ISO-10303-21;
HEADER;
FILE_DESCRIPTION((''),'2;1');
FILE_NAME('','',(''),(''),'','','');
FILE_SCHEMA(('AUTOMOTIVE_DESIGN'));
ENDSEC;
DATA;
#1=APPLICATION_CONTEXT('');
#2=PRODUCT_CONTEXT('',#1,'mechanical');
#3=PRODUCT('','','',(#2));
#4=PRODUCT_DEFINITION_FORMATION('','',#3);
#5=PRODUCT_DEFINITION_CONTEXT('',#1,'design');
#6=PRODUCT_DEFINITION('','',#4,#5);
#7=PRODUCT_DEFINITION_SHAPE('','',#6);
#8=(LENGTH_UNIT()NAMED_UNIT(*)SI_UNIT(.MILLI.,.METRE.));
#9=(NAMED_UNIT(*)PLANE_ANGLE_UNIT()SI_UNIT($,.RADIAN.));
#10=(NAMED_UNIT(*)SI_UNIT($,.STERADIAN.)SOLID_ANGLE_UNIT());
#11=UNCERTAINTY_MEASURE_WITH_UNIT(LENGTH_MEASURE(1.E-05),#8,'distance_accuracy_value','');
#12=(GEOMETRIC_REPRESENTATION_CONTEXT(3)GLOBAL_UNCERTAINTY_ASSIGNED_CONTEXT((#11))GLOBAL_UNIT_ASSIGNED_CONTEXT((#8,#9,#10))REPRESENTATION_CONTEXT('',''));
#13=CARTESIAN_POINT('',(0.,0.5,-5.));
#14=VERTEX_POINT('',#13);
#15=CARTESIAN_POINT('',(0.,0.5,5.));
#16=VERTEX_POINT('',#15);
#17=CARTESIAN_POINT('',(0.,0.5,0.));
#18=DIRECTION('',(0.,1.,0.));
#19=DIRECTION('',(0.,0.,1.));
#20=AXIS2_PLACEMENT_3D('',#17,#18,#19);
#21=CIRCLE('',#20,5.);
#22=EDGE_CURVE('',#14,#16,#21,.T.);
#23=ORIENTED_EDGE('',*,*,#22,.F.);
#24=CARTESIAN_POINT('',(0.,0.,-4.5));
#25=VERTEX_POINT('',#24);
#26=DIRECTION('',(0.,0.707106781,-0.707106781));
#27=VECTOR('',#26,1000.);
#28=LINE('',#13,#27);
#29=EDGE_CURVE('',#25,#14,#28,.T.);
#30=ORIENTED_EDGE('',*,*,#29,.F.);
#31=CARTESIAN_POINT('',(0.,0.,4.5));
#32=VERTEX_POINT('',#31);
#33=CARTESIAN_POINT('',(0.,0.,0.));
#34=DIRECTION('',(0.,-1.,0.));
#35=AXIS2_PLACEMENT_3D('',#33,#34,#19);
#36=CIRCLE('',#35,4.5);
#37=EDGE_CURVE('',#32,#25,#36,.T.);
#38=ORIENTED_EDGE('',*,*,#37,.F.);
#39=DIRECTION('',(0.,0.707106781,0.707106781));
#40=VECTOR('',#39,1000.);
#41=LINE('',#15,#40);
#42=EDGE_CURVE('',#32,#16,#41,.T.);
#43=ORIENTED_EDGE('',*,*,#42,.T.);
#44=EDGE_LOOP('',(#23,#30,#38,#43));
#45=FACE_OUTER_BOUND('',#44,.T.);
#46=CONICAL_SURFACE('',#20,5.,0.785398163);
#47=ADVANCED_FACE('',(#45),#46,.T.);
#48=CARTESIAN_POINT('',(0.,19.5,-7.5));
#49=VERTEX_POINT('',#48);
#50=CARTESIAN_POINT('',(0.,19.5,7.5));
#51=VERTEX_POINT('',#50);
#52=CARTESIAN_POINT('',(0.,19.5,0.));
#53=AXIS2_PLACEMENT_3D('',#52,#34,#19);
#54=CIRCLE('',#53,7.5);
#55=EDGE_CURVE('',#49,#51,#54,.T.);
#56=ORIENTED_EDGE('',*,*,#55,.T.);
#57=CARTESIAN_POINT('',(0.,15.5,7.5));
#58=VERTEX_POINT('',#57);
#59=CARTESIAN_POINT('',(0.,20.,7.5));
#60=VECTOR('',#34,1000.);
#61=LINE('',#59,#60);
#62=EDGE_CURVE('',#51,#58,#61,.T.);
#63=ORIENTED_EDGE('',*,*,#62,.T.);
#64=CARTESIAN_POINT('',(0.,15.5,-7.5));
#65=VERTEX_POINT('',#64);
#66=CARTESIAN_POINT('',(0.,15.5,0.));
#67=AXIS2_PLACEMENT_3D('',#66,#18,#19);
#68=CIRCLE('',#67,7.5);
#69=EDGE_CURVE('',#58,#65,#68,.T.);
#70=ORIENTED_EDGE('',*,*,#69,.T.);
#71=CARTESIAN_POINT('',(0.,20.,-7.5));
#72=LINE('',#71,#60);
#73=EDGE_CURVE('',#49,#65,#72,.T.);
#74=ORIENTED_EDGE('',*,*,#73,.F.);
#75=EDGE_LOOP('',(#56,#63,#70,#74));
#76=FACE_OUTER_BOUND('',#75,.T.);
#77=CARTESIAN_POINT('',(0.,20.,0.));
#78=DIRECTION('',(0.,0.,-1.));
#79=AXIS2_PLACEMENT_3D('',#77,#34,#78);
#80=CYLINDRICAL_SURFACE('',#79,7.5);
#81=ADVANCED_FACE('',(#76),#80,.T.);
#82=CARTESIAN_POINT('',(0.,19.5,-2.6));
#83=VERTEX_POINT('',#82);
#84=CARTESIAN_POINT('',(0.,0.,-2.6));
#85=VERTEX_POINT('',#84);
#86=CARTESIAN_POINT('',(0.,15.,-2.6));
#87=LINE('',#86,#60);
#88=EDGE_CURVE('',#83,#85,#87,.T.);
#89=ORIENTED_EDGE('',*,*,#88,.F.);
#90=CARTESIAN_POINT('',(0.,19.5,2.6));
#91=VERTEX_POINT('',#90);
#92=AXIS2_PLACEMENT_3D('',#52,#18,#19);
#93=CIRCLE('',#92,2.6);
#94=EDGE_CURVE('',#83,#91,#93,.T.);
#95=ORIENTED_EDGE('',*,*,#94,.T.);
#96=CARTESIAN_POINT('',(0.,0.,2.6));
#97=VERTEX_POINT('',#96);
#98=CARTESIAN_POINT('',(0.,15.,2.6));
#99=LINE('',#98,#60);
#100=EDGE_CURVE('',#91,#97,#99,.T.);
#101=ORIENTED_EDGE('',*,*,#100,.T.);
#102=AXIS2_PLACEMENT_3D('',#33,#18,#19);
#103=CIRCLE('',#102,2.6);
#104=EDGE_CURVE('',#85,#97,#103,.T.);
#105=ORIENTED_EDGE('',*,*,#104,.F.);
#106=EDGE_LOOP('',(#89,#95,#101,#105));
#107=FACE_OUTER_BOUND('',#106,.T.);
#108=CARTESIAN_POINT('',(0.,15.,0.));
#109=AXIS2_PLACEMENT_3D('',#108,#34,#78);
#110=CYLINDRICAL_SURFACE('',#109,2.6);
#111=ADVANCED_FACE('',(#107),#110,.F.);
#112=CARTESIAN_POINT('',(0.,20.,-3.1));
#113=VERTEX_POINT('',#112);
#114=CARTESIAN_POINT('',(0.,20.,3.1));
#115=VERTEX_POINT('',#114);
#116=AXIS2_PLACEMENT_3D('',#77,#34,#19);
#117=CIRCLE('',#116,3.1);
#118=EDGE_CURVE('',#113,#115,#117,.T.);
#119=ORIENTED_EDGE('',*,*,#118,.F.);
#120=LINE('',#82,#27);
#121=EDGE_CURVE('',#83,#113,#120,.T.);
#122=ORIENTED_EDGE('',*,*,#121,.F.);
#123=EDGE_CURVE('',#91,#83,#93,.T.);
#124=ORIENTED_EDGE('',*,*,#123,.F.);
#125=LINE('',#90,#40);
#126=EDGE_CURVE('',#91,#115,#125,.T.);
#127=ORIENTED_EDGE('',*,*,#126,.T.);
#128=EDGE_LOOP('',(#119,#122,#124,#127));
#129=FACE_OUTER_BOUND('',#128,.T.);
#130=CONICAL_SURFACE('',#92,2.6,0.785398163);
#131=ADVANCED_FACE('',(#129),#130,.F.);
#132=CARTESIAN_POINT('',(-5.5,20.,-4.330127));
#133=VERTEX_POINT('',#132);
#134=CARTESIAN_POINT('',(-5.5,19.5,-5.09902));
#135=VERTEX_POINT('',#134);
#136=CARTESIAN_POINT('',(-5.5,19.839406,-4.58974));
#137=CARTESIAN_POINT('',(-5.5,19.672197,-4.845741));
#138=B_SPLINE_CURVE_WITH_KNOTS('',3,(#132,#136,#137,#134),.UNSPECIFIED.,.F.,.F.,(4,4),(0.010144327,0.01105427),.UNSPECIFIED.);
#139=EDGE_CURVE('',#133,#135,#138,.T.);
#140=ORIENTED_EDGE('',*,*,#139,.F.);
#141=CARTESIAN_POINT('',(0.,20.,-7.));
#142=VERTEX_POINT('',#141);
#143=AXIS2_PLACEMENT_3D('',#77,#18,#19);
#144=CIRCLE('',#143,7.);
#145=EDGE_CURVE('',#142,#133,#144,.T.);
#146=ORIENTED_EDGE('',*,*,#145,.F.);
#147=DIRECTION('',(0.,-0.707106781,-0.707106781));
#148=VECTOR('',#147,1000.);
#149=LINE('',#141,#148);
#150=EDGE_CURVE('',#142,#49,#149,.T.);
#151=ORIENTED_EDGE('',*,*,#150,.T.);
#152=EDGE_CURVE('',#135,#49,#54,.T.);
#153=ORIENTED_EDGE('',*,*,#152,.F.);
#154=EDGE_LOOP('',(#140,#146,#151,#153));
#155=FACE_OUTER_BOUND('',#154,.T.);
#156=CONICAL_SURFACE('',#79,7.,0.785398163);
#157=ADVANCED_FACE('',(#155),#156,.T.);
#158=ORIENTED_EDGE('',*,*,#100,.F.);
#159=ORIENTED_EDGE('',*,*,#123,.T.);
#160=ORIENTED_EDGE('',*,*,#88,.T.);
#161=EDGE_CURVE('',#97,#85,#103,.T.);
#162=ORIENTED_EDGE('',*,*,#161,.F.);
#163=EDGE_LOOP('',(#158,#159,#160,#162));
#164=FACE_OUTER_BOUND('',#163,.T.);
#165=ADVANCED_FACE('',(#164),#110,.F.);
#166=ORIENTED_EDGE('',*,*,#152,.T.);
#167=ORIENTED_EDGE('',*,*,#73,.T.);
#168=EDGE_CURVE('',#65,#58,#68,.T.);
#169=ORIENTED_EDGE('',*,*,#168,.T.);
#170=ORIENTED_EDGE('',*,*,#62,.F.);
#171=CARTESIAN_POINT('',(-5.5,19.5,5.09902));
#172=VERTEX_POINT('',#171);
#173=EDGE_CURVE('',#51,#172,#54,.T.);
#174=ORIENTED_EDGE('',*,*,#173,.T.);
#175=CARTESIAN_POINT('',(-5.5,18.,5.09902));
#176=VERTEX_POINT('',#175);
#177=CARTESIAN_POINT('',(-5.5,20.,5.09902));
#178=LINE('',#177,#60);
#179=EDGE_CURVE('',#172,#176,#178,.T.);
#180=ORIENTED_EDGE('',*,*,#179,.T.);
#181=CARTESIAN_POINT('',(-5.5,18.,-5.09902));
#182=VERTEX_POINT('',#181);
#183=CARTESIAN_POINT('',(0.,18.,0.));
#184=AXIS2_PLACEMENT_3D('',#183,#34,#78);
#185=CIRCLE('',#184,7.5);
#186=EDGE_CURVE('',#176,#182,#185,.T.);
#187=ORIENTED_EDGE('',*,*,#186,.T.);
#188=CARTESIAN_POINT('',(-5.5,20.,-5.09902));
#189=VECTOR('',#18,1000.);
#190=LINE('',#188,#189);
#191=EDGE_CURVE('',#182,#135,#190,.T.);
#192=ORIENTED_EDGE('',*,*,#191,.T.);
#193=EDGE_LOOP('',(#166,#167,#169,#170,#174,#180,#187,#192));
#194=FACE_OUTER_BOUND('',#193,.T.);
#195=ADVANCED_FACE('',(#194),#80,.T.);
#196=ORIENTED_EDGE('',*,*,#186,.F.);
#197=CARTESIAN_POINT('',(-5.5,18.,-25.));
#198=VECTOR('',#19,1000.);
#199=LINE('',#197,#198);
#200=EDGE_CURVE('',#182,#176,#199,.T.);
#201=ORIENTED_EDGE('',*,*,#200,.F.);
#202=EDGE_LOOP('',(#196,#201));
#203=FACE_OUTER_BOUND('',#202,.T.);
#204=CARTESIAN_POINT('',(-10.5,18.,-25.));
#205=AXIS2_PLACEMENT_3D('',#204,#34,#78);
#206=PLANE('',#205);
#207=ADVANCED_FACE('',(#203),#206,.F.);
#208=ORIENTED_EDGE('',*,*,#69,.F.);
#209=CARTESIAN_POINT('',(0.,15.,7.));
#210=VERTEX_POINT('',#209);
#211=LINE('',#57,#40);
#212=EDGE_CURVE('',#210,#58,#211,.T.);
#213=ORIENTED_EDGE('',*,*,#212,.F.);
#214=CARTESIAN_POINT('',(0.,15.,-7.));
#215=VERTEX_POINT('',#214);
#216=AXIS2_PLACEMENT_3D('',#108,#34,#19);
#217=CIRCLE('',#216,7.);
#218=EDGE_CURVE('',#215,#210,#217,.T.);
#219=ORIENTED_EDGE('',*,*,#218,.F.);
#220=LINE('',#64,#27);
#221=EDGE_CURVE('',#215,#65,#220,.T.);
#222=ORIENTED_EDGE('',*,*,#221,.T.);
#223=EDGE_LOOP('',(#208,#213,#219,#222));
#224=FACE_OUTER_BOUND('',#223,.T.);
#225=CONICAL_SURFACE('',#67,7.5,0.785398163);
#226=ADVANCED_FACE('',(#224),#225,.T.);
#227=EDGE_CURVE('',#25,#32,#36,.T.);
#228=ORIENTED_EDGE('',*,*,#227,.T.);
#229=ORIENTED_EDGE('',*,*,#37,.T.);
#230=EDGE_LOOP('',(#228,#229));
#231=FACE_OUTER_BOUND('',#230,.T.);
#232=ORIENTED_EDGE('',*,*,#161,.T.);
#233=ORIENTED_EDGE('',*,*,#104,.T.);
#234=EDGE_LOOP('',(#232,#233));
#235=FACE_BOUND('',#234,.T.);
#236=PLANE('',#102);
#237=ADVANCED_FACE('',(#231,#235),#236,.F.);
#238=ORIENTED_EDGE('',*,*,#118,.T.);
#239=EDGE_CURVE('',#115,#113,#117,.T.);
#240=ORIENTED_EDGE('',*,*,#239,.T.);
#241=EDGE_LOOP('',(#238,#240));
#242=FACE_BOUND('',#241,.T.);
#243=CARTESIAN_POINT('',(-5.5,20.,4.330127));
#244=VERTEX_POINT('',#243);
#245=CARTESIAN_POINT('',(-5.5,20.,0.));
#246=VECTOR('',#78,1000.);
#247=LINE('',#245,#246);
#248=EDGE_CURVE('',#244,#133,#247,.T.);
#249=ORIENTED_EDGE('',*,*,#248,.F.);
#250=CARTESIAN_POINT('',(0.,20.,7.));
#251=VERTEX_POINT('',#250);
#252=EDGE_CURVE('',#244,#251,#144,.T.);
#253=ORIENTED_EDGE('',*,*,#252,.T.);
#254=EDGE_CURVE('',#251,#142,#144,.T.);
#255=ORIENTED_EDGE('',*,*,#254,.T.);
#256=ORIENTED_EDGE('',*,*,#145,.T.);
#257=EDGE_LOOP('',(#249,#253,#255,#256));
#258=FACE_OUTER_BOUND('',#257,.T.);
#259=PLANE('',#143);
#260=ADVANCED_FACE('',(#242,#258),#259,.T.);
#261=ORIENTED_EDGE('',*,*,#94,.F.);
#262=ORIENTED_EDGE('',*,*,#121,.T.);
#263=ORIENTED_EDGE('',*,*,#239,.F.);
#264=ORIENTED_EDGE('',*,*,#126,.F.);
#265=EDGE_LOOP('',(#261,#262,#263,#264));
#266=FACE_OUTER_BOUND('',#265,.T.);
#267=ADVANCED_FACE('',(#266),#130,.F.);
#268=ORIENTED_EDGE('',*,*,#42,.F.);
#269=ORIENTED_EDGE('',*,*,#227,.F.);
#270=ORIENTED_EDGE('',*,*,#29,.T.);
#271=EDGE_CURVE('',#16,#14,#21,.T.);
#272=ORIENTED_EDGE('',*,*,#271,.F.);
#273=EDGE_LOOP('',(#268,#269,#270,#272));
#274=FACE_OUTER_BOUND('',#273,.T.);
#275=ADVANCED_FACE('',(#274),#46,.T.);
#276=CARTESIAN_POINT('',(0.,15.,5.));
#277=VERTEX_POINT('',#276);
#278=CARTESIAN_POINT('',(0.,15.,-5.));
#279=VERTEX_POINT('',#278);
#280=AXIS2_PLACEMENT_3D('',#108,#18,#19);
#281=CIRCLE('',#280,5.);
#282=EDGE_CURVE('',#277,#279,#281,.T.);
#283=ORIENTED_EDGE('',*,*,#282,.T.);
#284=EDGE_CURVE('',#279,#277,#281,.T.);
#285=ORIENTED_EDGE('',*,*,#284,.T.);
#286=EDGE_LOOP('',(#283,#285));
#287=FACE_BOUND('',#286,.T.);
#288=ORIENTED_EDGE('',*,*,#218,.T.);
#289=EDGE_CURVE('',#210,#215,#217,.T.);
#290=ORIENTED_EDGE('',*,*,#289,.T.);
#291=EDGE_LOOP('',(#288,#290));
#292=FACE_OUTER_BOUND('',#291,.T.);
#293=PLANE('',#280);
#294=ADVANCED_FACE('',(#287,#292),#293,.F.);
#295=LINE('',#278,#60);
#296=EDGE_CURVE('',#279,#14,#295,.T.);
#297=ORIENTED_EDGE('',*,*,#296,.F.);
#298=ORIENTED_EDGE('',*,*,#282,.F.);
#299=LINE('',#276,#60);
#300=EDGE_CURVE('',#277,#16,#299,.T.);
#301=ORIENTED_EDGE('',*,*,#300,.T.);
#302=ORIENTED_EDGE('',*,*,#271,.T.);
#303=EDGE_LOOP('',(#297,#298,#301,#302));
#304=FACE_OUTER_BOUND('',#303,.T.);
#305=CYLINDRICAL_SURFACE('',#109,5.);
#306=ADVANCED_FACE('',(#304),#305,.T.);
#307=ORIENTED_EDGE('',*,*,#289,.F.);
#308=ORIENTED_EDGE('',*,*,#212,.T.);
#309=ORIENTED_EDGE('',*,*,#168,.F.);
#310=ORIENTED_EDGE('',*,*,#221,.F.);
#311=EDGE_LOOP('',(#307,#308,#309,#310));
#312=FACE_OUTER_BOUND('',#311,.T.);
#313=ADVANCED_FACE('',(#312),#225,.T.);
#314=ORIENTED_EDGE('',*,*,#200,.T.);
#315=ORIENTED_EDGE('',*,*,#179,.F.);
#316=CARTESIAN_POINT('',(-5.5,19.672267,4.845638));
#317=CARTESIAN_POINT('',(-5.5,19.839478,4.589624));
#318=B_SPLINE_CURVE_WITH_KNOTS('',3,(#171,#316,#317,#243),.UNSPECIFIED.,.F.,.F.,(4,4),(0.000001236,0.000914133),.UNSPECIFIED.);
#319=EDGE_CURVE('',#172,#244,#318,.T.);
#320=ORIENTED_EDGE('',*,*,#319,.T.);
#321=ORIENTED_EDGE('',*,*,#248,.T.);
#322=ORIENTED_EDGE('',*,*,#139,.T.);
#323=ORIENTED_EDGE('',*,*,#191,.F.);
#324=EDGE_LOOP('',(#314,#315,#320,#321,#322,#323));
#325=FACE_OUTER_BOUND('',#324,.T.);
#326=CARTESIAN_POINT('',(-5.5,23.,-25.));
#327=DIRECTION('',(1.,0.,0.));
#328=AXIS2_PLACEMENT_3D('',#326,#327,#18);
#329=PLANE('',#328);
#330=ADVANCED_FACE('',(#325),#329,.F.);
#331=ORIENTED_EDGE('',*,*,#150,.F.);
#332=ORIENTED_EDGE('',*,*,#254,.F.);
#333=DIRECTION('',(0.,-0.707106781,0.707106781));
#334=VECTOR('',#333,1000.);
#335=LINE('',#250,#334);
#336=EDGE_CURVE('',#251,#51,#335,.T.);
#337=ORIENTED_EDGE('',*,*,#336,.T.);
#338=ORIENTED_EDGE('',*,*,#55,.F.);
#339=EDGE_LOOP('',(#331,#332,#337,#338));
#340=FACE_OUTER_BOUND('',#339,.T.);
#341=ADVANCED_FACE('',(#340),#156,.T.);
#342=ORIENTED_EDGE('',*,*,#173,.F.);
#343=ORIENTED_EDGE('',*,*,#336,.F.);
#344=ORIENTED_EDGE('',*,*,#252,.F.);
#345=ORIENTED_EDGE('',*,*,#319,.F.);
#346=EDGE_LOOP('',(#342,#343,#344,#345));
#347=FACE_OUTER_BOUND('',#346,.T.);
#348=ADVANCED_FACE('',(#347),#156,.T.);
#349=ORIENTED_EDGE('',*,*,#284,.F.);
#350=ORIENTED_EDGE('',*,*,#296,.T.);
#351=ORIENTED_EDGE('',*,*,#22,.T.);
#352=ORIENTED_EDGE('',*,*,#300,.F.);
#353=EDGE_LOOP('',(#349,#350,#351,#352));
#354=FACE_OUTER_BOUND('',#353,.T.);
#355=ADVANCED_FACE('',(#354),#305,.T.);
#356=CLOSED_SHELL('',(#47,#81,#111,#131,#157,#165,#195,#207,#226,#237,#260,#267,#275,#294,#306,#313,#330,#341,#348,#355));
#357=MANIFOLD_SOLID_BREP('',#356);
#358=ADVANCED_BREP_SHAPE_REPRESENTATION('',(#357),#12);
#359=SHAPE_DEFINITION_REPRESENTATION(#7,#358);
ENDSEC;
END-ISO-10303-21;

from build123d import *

# Parameters (mm, degrees)
SKETCH1_R           = 5
SKETCH1_R_2         = 2.6
BOSS_EXTRUDE1_DEPTH = 15
SKETCH2_R           = 7.5
SKETCH2_R_2         = 2.6
BOSS_EXTRUDE2_DEPTH = 5
CHAMFER1_SIZE       = 0.5
SKETCH3_W           = 5
SKETCH3_H           = 5
CUT_EXTRUDE1_DEPTH  = 25


with BuildPart() as part:
    # Sketch1 → Boss-Extrude1 (new body)
    with BuildSketch(Plane(origin=(0, 0, 0), x_dir=(1, 0, 0), z_dir=(0, 1, 0))):
        with Locations(Location((0, 0, 0), (0, 0, 270))):
            Circle(SKETCH1_R)
        with Locations(Location((0, 0, 0), (0, 0, 270))):
            Circle(SKETCH1_R_2, mode=Mode.SUBTRACT)
    extrude(amount=BOSS_EXTRUDE1_DEPTH)

    # Sketch2 → Boss-Extrude2 (add)
    with BuildSketch(Plane(origin=(0, 15, 0), x_dir=(1, 0, 0), z_dir=(0, 1, 0))):
        with Locations(Location((0, 0, 0), (0, 0, 270))):
            Circle(SKETCH2_R)
        with Locations(Location((0, 0, 0), (0, 0, 270))):
            Circle(SKETCH2_R_2, mode=Mode.SUBTRACT)
    extrude(amount=BOSS_EXTRUDE2_DEPTH)

    # Chamfer1
    chamfer1_edges = [part.edges().sort_by_distance(p)[0] for p in [
        (0, 20, -7.5),
        (0, 15, -7.5),
        (0, 20, -2.6),
        (0, 0, -5),
    ]]
    chamfer(chamfer1_edges, length=CHAMFER1_SIZE)

    # Sketch3 → Cut-Extrude1 (cut, symmetric)
    with BuildSketch(Plane.XY):
        with Locations((-8, 20.5)):
            Rectangle(SKETCH3_W, SKETCH3_H)
    extrude(amount=CUT_EXTRUDE1_DEPTH, both=True, mode=Mode.SUBTRACT)


solid = part.part
